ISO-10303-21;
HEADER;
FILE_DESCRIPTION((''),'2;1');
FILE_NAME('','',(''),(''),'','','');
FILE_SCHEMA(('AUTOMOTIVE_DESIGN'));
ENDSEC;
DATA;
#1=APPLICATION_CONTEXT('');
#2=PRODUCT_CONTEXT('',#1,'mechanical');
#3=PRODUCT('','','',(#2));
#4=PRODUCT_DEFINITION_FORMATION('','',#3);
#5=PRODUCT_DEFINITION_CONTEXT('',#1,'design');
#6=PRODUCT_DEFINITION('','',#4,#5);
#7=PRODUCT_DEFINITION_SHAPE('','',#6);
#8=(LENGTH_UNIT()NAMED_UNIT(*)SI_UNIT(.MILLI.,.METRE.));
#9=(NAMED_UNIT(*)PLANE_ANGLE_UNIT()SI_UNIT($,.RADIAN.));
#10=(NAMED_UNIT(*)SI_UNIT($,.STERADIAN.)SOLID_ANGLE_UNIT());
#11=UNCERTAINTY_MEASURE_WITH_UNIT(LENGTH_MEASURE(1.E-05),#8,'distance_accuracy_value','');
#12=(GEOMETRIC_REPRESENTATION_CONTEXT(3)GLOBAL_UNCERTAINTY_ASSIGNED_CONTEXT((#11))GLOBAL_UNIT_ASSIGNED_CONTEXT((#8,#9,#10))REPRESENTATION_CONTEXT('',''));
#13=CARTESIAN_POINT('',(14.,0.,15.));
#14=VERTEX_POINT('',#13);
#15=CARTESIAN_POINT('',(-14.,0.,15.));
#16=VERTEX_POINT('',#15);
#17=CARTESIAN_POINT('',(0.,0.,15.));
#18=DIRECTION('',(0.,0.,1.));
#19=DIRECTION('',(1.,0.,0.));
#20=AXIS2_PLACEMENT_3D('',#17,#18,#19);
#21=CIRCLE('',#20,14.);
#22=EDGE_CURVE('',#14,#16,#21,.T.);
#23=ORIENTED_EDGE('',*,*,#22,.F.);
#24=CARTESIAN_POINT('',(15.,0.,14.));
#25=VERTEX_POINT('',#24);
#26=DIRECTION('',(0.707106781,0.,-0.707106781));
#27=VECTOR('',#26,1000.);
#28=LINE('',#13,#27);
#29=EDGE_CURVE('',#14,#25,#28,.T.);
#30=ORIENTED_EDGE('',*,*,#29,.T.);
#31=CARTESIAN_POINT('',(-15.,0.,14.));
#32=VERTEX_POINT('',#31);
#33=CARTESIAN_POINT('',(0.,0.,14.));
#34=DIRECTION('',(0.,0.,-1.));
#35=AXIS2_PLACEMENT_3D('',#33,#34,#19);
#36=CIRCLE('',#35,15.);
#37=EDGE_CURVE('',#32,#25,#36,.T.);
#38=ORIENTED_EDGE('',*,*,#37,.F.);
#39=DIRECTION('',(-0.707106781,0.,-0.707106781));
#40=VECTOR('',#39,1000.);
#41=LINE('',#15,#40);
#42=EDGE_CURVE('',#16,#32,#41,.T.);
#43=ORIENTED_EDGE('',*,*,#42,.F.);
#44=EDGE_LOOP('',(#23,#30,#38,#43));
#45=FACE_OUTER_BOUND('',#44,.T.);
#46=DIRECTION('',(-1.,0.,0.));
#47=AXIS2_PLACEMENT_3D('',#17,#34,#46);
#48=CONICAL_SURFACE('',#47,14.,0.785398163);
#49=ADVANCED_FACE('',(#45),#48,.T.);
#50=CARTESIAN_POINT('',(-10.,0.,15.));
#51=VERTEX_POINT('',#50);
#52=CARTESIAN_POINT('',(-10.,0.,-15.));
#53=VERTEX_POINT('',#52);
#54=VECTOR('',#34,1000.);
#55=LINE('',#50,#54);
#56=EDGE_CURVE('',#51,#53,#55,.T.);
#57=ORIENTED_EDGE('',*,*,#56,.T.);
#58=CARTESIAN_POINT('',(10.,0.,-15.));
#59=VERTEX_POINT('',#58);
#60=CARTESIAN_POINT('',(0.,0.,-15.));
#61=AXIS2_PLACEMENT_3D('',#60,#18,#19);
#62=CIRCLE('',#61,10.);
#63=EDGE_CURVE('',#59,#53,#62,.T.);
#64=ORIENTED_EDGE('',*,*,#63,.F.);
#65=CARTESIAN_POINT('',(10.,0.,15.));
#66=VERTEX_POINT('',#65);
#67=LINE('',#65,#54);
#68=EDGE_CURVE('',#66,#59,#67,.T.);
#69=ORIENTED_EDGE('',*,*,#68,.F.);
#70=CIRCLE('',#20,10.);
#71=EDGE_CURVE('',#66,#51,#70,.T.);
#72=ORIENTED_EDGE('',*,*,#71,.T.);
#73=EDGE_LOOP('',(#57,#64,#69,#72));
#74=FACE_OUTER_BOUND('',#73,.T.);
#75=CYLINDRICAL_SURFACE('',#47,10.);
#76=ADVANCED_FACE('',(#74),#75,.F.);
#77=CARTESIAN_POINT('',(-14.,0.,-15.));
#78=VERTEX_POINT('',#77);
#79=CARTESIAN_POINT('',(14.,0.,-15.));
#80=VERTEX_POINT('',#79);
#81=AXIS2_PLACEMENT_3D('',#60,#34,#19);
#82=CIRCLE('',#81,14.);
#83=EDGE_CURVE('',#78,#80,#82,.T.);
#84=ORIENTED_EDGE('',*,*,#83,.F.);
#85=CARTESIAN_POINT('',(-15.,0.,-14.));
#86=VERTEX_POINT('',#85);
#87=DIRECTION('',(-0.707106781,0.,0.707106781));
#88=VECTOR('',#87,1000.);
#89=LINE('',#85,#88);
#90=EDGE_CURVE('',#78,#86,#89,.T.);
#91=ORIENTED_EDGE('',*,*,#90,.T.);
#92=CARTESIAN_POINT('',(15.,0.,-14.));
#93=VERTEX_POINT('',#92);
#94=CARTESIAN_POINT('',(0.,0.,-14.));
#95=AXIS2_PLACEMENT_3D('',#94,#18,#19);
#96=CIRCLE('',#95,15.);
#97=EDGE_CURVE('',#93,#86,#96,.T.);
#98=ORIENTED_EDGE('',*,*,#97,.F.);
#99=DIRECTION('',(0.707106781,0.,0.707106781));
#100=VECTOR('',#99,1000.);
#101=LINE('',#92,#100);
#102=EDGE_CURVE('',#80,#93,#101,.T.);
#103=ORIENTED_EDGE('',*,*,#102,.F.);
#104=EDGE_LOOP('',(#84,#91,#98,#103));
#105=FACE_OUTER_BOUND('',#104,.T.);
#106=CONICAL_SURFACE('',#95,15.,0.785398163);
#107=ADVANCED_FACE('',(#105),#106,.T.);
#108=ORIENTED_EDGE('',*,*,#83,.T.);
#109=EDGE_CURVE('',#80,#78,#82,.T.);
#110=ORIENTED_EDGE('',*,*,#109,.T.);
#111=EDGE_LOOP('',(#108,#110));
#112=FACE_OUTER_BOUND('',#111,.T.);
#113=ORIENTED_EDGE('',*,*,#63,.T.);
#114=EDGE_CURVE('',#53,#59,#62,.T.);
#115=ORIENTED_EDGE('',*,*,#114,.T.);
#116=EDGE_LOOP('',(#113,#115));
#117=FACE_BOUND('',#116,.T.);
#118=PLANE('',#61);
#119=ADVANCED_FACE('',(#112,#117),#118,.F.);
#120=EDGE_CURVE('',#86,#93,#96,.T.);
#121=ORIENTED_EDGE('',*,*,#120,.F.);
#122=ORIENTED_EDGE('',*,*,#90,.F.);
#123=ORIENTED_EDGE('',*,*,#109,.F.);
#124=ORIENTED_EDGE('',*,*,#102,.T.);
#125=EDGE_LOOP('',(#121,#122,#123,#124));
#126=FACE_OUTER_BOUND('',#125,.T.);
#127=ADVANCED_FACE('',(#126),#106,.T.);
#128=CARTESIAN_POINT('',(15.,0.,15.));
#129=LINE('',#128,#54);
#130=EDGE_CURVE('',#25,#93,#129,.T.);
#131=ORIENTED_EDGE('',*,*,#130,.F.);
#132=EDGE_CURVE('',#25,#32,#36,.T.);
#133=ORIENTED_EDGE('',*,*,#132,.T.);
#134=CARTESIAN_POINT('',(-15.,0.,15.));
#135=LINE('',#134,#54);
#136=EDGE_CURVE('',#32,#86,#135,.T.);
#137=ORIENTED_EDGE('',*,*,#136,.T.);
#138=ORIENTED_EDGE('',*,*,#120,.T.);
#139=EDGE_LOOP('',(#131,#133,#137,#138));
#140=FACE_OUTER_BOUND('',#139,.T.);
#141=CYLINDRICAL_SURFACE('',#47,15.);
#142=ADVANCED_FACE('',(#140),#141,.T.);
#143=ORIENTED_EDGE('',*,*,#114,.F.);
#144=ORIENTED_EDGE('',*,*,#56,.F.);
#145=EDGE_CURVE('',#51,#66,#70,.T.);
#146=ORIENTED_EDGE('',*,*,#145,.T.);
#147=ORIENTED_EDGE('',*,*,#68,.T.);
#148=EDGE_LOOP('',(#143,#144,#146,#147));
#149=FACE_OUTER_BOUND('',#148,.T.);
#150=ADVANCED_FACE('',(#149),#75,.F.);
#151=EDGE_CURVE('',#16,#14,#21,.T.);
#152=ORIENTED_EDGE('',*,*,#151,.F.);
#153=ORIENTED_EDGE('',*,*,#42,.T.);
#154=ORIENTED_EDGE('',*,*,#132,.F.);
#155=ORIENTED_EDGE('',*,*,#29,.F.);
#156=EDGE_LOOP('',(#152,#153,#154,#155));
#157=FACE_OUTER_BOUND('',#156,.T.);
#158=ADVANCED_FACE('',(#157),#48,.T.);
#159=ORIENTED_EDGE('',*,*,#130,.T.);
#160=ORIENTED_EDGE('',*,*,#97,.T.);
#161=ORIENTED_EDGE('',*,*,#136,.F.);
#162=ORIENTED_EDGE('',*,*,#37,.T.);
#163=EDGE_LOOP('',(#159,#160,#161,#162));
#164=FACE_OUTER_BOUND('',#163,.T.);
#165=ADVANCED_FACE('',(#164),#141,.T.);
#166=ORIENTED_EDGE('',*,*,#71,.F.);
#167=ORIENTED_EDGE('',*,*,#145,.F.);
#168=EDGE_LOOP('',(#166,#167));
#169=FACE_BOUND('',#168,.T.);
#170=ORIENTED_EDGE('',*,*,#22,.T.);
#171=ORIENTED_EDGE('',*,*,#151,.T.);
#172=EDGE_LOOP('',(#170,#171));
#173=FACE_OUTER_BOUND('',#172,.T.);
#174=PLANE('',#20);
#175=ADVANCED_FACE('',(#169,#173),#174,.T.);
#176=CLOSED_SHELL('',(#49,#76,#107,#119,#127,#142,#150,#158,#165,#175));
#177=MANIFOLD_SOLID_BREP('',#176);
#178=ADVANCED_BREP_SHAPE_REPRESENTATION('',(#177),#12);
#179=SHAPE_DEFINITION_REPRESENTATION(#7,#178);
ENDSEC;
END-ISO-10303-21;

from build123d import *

# Parameters (mm, degrees)
BUSHING_PROFILE_30_20_R       = 15
BUSHING_PROFILE_30_20_R_2     = 10
BUSHING_BODY_L30_DEPTH        = 15
OUTER_EDGE_CHAMFERS_1X45_SIZE = 1


with BuildPart() as part:
    # Bushing Profile Ø30-Ø20 → Bushing Body L30 (new, symmetric)
    with BuildSketch(Plane.XY):
        Circle(BUSHING_PROFILE_30_20_R)
        Circle(BUSHING_PROFILE_30_20_R_2, mode=Mode.SUBTRACT)
    extrude(amount=BUSHING_BODY_L30_DEPTH, both=True)

    # Outer Edge Chamfers 1x45°
    outer_edge_chamfers_1x45_edges = [part.edges().sort_by_distance(p)[0] for p in [
        (-15, 0, -15),
        (-15, 0, 15),
    ]]
    chamfer(outer_edge_chamfers_1x45_edges, length=OUTER_EDGE_CHAMFERS_1X45_SIZE)


solid = part.part
